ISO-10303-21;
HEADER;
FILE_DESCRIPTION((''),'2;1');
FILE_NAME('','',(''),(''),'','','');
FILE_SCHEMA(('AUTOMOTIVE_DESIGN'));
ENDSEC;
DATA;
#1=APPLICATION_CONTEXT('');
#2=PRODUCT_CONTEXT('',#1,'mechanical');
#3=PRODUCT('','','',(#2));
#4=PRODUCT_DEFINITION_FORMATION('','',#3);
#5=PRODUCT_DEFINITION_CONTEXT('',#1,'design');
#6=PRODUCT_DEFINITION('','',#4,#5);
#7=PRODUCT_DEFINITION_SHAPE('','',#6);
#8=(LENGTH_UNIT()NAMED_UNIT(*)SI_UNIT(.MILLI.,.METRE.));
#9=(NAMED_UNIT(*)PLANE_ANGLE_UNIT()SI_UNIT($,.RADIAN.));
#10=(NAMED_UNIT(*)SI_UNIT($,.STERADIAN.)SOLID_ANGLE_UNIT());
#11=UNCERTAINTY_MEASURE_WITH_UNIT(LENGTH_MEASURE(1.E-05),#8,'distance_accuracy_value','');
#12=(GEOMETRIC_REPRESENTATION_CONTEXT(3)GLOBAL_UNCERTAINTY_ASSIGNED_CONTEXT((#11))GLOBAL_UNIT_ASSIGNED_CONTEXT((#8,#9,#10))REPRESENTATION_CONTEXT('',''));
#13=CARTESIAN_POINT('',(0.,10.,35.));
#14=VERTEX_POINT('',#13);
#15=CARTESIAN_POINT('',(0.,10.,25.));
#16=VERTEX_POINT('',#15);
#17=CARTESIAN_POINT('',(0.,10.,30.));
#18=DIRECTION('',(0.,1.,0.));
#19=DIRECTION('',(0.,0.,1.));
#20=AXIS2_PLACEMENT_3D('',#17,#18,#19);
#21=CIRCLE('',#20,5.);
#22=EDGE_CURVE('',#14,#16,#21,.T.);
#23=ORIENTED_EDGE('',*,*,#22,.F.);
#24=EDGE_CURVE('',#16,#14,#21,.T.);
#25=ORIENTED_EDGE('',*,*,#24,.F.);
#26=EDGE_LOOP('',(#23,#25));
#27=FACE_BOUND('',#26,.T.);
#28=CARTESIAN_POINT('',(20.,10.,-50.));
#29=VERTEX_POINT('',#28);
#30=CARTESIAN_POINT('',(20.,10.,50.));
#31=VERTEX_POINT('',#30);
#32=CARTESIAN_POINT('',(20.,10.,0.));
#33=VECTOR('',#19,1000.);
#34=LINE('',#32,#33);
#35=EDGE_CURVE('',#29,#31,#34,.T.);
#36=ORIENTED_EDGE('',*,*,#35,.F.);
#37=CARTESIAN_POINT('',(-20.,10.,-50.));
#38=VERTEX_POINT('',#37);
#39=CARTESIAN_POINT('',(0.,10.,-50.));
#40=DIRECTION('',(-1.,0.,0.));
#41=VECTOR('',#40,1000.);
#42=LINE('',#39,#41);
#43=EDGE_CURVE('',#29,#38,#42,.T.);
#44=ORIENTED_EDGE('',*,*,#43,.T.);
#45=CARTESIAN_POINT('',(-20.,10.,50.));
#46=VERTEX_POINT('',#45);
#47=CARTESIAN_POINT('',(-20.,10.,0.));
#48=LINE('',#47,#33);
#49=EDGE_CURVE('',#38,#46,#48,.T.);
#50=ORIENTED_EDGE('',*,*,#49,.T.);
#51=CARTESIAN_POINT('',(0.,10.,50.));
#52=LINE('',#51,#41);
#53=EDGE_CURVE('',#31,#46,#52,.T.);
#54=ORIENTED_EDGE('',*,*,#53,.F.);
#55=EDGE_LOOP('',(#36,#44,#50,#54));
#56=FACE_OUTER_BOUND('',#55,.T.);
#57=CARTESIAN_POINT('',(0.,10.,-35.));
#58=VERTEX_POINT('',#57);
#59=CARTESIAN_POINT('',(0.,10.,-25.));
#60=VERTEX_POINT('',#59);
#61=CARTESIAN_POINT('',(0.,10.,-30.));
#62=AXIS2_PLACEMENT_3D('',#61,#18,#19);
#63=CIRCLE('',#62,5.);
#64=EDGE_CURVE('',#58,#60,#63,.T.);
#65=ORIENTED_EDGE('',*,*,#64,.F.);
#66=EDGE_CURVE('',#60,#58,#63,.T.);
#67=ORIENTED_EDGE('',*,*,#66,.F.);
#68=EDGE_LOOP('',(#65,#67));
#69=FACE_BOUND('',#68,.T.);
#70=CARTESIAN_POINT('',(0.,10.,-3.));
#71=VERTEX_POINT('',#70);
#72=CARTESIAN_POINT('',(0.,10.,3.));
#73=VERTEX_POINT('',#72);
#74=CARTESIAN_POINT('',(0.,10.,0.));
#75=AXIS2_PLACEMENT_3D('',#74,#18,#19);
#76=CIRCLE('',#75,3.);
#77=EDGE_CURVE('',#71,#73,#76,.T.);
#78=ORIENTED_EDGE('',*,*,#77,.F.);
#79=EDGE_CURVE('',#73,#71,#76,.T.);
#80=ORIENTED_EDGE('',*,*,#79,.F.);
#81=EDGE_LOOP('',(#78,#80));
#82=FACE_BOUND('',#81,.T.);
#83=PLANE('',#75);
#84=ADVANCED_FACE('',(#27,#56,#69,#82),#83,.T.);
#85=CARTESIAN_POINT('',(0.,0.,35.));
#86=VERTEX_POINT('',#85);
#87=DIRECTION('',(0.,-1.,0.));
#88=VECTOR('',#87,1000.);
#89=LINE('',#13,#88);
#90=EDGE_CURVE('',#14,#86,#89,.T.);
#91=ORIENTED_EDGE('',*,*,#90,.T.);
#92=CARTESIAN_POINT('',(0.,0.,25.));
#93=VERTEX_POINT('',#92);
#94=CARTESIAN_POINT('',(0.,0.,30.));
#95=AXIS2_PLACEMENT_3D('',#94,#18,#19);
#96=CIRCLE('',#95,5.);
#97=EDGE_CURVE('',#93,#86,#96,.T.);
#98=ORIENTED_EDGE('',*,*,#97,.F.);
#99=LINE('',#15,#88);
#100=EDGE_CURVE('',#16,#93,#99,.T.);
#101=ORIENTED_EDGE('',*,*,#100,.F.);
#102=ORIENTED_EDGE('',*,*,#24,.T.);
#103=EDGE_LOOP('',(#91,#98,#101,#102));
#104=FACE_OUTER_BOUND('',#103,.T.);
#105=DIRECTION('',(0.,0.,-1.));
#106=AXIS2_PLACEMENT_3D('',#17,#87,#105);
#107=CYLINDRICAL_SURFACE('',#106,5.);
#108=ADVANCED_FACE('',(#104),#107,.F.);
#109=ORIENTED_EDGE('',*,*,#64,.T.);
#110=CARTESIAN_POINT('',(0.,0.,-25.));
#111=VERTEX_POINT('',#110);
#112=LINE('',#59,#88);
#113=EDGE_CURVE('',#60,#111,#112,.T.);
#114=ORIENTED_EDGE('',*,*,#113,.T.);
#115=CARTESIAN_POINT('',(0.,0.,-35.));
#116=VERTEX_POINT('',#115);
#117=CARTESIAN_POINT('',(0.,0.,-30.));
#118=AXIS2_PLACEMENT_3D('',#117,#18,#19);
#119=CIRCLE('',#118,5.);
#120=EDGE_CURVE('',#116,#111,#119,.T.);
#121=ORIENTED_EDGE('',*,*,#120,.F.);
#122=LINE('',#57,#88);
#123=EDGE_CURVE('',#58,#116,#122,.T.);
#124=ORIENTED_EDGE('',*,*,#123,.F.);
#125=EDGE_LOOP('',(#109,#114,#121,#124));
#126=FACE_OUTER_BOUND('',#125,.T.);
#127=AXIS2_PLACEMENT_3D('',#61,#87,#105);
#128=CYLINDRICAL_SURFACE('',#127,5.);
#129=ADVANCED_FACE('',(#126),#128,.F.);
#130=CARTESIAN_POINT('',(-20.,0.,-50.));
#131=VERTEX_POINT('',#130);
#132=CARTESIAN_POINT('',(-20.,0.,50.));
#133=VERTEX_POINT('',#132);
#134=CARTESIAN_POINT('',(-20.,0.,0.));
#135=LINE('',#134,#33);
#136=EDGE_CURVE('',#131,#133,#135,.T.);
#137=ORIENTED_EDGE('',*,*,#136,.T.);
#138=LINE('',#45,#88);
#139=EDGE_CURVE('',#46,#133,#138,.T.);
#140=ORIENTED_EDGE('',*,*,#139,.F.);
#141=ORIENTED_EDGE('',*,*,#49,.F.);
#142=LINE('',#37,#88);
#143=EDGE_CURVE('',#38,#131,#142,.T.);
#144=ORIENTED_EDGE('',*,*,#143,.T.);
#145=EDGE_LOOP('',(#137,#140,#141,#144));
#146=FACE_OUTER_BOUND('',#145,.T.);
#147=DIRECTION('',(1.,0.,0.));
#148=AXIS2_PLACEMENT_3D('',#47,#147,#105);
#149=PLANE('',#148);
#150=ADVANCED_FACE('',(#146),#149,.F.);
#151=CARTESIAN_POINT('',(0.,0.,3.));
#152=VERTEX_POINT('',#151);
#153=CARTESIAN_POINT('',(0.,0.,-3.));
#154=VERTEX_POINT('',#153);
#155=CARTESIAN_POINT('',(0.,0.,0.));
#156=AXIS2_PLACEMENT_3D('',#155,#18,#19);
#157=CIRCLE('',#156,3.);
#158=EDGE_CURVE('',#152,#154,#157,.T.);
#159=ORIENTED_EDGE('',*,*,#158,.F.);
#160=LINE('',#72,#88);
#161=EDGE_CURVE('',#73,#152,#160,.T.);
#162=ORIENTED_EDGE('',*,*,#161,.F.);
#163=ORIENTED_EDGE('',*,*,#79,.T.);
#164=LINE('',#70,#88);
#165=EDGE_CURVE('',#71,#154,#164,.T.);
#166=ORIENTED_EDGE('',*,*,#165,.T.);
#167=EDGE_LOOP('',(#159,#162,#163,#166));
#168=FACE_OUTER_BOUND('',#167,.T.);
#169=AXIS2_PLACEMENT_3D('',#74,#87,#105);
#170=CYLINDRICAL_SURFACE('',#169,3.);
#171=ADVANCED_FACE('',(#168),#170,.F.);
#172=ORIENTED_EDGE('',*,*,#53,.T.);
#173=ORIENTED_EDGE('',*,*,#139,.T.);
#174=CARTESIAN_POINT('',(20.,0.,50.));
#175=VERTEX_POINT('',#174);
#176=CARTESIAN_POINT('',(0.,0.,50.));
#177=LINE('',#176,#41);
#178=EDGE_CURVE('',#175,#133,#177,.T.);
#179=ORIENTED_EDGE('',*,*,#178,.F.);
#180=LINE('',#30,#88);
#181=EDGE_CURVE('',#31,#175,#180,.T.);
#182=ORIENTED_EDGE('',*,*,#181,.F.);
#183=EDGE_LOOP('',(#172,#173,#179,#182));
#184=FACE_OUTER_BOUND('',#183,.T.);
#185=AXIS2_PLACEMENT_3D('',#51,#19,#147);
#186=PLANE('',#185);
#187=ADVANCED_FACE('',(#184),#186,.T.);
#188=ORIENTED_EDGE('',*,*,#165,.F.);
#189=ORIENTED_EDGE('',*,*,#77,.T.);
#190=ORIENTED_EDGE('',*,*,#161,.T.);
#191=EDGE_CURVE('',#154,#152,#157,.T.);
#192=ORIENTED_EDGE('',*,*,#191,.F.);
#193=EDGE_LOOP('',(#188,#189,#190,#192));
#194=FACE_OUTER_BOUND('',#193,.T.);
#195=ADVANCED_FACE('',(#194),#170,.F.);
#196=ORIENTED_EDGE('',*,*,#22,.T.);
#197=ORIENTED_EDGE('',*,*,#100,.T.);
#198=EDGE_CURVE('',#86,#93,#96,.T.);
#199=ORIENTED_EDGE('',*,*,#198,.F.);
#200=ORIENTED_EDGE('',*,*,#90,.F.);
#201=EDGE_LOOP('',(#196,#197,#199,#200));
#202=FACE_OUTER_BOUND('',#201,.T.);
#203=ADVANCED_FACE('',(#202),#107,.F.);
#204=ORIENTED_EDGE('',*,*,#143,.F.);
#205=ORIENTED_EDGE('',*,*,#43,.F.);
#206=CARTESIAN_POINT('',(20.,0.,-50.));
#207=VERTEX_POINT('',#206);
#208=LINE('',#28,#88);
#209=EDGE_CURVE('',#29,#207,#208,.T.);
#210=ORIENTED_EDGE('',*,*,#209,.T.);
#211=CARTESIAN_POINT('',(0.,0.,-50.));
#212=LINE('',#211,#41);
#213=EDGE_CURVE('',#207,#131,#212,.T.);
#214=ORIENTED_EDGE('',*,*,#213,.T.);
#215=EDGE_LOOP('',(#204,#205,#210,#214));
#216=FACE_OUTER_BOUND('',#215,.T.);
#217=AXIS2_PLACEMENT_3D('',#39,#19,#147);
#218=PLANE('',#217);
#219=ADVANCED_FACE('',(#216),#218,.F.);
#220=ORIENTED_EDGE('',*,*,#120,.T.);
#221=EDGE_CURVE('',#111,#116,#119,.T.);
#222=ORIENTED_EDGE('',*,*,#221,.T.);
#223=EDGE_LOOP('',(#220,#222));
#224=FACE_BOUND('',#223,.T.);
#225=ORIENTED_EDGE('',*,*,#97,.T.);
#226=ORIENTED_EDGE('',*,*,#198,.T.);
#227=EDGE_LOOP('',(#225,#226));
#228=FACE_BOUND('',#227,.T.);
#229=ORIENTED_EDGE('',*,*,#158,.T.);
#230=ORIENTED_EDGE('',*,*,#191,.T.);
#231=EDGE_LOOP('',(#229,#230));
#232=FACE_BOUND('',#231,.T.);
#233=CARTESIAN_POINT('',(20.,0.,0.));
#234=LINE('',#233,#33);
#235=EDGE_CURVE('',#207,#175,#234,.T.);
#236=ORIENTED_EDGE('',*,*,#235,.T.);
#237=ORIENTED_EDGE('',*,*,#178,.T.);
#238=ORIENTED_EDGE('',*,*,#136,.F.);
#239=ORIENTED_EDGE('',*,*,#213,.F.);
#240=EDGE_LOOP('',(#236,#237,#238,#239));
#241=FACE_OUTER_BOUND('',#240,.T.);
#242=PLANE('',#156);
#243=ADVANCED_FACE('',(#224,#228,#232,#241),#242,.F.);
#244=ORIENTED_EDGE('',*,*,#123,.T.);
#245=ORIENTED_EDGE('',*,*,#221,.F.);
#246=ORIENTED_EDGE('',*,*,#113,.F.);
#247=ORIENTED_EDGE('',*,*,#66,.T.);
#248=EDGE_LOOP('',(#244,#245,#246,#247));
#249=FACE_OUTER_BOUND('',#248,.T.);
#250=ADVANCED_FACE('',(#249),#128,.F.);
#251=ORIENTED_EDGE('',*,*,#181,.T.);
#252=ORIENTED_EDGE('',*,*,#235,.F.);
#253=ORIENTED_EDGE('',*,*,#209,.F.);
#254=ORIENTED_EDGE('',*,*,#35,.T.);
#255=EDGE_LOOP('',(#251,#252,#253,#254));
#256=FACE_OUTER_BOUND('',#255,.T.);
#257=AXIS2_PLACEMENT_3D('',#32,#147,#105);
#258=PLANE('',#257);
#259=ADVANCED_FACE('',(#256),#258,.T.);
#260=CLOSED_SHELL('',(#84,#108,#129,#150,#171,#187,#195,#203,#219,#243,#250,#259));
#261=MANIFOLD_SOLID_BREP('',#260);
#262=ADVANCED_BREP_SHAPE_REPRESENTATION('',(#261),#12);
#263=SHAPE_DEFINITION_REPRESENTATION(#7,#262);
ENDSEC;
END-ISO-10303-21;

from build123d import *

# Parameters (mm, degrees)
SKETCH1_W           = 40
SKETCH1_H           = 100
SKETCH1_R           = 5
SKETCH1_R_2         = 3
BOSS_EXTRUDE1_DEPTH = 10


with BuildPart() as part:
    # Sketch1 → Boss-Extrude1 (new body)
    with BuildSketch(Plane(origin=(0, 0, 0), x_dir=(1, 0, 0), z_dir=(0, 1, 0))):
        Rectangle(SKETCH1_W, SKETCH1_H)
        with Locations(Location((0, 30, 0), (0, 0, 270))):
            Circle(SKETCH1_R, mode=Mode.SUBTRACT)
        with Locations(Location((0, -30, 0), (0, 0, 270))):
            Circle(SKETCH1_R, mode=Mode.SUBTRACT)
        with Locations(Location((0, 0, 0), (0, 0, 270))):
            Circle(SKETCH1_R_2, mode=Mode.SUBTRACT)
    extrude(amount=BOSS_EXTRUDE1_DEPTH)


solid = part.part
